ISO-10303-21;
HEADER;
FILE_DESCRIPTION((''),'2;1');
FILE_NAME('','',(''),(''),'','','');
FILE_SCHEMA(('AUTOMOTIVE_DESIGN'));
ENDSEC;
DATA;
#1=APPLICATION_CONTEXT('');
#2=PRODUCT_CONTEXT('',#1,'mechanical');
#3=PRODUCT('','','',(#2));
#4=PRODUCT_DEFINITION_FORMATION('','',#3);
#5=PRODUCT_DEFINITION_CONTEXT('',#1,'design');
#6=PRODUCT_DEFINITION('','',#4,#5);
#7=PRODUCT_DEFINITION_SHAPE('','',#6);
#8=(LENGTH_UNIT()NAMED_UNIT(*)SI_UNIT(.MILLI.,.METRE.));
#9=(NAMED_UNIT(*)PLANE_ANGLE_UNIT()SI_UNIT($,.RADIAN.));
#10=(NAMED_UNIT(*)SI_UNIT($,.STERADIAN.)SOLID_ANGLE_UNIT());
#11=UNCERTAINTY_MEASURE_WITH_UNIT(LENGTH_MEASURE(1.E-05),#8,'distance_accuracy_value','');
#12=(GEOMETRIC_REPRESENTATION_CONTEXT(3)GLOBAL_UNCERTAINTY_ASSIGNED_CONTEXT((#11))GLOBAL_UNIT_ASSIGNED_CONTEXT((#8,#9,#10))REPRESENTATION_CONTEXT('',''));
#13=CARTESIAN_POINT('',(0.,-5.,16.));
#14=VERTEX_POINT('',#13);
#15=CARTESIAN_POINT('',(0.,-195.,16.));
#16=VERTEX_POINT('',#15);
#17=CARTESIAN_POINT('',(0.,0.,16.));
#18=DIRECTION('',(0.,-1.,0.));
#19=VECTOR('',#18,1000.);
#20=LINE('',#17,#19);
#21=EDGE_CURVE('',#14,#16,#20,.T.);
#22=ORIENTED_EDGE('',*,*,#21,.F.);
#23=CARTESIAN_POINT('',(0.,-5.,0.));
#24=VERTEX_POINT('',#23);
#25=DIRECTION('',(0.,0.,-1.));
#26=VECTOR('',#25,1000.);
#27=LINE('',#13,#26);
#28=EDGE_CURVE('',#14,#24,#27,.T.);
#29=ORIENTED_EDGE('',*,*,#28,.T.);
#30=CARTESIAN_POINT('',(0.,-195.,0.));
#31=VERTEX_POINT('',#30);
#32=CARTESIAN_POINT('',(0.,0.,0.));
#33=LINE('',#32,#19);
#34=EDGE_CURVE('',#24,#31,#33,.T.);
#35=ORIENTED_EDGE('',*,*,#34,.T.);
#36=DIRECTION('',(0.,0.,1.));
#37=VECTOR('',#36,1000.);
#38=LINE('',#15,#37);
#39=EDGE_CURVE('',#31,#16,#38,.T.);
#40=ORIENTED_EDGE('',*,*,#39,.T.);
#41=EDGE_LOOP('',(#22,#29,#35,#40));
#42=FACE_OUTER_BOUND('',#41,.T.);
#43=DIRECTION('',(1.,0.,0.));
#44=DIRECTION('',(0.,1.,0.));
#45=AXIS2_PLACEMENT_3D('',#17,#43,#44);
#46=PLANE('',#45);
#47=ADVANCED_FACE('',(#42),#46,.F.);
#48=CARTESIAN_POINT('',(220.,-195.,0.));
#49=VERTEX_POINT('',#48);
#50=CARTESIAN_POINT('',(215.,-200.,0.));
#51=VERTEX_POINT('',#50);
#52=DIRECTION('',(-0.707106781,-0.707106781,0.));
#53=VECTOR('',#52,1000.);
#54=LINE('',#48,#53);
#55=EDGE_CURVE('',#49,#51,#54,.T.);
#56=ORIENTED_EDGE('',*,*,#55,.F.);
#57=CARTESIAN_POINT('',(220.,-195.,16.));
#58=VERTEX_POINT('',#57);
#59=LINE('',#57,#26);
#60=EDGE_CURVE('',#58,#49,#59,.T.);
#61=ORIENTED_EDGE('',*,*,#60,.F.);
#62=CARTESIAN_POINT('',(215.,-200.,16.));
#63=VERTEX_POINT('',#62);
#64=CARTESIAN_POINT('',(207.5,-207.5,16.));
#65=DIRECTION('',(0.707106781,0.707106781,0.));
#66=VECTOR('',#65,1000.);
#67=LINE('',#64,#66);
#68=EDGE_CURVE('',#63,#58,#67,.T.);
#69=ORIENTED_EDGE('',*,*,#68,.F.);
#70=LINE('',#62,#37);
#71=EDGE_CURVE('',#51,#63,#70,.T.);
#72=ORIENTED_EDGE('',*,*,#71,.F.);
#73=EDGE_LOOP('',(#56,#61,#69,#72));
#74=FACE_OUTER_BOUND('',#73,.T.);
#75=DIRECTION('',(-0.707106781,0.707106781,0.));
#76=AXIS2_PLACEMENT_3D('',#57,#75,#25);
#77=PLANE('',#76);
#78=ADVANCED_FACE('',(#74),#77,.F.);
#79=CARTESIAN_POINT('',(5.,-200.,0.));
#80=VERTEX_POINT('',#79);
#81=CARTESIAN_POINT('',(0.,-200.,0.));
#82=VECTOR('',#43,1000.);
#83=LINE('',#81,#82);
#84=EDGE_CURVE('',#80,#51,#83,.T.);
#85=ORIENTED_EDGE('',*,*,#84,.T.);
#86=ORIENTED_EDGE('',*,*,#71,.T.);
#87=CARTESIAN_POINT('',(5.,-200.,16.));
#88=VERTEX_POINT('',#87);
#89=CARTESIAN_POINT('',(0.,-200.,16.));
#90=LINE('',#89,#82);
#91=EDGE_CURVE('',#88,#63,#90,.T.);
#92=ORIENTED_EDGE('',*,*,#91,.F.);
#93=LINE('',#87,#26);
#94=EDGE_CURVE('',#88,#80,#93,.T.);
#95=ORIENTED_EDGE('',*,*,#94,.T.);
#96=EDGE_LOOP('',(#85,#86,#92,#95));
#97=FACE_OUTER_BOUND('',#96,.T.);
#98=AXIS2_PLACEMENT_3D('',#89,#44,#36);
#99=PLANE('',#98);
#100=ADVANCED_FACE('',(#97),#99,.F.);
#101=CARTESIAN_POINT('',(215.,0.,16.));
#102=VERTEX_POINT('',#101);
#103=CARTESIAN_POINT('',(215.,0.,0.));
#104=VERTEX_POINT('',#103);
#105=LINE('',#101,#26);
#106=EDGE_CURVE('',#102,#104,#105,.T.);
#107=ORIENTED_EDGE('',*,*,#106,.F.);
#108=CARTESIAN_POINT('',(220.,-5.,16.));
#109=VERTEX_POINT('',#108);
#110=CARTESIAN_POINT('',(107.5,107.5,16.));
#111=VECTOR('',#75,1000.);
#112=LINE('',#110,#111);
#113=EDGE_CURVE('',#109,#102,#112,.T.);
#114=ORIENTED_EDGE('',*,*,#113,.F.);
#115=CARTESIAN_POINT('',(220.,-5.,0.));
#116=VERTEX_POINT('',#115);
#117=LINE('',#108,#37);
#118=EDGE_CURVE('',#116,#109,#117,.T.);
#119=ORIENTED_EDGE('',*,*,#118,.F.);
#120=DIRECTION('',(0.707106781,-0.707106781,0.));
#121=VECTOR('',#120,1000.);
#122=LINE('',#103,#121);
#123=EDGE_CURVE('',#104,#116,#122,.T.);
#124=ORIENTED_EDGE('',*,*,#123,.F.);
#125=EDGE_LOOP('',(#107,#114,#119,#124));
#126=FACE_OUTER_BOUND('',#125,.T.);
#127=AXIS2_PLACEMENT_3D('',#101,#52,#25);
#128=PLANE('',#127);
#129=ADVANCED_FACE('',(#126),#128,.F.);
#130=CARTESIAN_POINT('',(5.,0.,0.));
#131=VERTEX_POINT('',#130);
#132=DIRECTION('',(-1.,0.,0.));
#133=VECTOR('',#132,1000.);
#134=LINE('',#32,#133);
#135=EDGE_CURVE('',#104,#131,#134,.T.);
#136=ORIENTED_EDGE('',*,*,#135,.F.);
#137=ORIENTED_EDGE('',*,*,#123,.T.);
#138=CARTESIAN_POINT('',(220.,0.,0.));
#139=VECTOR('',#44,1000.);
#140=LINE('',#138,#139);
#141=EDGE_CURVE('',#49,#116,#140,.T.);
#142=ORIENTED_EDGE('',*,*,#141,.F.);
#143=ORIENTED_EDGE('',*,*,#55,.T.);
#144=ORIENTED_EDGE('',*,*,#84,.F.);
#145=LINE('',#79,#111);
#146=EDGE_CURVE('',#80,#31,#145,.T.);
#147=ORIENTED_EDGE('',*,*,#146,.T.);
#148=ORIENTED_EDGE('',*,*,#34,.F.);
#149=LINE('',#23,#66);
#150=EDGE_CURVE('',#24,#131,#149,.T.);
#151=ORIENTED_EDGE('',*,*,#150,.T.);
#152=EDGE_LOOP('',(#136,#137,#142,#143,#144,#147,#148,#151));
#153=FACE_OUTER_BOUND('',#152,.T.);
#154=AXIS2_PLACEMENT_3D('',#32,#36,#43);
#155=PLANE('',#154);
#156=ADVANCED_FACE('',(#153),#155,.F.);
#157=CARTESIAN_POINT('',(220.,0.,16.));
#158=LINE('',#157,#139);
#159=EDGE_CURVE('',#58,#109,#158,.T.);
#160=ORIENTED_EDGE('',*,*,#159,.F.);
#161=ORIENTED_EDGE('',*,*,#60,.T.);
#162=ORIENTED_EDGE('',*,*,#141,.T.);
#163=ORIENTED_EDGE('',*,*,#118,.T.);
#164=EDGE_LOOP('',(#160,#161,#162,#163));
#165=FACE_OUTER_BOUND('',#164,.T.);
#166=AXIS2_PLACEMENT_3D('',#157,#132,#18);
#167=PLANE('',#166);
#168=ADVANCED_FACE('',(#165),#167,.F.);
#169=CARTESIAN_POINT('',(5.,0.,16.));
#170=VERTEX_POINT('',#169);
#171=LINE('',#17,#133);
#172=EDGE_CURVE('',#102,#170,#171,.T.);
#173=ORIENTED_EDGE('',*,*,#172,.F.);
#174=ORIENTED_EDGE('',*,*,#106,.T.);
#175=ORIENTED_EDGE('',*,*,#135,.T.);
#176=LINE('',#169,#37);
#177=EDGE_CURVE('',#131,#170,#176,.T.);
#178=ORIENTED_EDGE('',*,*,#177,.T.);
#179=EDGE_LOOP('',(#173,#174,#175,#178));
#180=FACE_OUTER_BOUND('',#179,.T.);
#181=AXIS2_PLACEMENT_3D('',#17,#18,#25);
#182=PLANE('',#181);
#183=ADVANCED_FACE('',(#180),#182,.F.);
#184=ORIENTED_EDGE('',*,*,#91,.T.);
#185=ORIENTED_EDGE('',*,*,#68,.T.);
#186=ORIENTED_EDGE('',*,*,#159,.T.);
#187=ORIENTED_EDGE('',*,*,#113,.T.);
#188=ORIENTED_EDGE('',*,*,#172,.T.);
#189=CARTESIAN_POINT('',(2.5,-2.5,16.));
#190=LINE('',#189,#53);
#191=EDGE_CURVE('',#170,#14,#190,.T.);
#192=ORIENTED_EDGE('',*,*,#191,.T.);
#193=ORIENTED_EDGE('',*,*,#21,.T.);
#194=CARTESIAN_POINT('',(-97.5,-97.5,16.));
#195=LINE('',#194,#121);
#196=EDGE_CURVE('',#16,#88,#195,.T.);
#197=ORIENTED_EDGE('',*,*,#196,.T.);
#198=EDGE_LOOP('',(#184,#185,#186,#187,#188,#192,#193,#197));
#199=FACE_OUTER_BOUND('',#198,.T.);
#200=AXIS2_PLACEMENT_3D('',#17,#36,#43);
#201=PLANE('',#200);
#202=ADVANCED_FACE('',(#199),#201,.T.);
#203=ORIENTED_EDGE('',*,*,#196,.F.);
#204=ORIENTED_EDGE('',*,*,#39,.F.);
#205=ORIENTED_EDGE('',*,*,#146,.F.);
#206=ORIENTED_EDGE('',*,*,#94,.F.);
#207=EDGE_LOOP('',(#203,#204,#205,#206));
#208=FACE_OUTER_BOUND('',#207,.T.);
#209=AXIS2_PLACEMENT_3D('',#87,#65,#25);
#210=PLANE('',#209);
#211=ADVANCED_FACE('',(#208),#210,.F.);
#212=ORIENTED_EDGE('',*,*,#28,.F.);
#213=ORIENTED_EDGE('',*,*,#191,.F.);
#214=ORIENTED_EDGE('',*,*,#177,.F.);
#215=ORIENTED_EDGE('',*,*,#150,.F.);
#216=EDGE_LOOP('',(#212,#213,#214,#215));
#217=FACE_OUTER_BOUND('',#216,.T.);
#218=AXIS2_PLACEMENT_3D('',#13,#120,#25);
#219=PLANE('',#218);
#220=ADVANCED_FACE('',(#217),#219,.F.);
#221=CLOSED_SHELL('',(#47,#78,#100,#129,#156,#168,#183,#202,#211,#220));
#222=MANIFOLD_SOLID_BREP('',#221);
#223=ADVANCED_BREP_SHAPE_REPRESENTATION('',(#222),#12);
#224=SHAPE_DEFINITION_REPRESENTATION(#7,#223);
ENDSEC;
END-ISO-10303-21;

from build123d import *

# Parameters (mm, degrees)
SKETCH_1_W      = 220
SKETCH_1_H      = 200
EXTRUDE_1_DEPTH = 16
CHAMFER_1_SIZE  = 5


with BuildPart() as part:
    # 草图1 → 凸台-拉伸1 (new body)
    with BuildSketch(Plane.XY):
        with Locations((110, -100)):
            Rectangle(SKETCH_1_W, SKETCH_1_H)
    extrude(amount=EXTRUDE_1_DEPTH)

    # 倒角1
    chamfer_1_edges = [part.edges().sort_by_distance(p)[0] for p in [
        (0, 0, 8),
        (220, 0, 8),
        (220, -200, 8),
        (0, -200, 8),
    ]]
    chamfer(chamfer_1_edges, length=CHAMFER_1_SIZE)


solid = part.part
